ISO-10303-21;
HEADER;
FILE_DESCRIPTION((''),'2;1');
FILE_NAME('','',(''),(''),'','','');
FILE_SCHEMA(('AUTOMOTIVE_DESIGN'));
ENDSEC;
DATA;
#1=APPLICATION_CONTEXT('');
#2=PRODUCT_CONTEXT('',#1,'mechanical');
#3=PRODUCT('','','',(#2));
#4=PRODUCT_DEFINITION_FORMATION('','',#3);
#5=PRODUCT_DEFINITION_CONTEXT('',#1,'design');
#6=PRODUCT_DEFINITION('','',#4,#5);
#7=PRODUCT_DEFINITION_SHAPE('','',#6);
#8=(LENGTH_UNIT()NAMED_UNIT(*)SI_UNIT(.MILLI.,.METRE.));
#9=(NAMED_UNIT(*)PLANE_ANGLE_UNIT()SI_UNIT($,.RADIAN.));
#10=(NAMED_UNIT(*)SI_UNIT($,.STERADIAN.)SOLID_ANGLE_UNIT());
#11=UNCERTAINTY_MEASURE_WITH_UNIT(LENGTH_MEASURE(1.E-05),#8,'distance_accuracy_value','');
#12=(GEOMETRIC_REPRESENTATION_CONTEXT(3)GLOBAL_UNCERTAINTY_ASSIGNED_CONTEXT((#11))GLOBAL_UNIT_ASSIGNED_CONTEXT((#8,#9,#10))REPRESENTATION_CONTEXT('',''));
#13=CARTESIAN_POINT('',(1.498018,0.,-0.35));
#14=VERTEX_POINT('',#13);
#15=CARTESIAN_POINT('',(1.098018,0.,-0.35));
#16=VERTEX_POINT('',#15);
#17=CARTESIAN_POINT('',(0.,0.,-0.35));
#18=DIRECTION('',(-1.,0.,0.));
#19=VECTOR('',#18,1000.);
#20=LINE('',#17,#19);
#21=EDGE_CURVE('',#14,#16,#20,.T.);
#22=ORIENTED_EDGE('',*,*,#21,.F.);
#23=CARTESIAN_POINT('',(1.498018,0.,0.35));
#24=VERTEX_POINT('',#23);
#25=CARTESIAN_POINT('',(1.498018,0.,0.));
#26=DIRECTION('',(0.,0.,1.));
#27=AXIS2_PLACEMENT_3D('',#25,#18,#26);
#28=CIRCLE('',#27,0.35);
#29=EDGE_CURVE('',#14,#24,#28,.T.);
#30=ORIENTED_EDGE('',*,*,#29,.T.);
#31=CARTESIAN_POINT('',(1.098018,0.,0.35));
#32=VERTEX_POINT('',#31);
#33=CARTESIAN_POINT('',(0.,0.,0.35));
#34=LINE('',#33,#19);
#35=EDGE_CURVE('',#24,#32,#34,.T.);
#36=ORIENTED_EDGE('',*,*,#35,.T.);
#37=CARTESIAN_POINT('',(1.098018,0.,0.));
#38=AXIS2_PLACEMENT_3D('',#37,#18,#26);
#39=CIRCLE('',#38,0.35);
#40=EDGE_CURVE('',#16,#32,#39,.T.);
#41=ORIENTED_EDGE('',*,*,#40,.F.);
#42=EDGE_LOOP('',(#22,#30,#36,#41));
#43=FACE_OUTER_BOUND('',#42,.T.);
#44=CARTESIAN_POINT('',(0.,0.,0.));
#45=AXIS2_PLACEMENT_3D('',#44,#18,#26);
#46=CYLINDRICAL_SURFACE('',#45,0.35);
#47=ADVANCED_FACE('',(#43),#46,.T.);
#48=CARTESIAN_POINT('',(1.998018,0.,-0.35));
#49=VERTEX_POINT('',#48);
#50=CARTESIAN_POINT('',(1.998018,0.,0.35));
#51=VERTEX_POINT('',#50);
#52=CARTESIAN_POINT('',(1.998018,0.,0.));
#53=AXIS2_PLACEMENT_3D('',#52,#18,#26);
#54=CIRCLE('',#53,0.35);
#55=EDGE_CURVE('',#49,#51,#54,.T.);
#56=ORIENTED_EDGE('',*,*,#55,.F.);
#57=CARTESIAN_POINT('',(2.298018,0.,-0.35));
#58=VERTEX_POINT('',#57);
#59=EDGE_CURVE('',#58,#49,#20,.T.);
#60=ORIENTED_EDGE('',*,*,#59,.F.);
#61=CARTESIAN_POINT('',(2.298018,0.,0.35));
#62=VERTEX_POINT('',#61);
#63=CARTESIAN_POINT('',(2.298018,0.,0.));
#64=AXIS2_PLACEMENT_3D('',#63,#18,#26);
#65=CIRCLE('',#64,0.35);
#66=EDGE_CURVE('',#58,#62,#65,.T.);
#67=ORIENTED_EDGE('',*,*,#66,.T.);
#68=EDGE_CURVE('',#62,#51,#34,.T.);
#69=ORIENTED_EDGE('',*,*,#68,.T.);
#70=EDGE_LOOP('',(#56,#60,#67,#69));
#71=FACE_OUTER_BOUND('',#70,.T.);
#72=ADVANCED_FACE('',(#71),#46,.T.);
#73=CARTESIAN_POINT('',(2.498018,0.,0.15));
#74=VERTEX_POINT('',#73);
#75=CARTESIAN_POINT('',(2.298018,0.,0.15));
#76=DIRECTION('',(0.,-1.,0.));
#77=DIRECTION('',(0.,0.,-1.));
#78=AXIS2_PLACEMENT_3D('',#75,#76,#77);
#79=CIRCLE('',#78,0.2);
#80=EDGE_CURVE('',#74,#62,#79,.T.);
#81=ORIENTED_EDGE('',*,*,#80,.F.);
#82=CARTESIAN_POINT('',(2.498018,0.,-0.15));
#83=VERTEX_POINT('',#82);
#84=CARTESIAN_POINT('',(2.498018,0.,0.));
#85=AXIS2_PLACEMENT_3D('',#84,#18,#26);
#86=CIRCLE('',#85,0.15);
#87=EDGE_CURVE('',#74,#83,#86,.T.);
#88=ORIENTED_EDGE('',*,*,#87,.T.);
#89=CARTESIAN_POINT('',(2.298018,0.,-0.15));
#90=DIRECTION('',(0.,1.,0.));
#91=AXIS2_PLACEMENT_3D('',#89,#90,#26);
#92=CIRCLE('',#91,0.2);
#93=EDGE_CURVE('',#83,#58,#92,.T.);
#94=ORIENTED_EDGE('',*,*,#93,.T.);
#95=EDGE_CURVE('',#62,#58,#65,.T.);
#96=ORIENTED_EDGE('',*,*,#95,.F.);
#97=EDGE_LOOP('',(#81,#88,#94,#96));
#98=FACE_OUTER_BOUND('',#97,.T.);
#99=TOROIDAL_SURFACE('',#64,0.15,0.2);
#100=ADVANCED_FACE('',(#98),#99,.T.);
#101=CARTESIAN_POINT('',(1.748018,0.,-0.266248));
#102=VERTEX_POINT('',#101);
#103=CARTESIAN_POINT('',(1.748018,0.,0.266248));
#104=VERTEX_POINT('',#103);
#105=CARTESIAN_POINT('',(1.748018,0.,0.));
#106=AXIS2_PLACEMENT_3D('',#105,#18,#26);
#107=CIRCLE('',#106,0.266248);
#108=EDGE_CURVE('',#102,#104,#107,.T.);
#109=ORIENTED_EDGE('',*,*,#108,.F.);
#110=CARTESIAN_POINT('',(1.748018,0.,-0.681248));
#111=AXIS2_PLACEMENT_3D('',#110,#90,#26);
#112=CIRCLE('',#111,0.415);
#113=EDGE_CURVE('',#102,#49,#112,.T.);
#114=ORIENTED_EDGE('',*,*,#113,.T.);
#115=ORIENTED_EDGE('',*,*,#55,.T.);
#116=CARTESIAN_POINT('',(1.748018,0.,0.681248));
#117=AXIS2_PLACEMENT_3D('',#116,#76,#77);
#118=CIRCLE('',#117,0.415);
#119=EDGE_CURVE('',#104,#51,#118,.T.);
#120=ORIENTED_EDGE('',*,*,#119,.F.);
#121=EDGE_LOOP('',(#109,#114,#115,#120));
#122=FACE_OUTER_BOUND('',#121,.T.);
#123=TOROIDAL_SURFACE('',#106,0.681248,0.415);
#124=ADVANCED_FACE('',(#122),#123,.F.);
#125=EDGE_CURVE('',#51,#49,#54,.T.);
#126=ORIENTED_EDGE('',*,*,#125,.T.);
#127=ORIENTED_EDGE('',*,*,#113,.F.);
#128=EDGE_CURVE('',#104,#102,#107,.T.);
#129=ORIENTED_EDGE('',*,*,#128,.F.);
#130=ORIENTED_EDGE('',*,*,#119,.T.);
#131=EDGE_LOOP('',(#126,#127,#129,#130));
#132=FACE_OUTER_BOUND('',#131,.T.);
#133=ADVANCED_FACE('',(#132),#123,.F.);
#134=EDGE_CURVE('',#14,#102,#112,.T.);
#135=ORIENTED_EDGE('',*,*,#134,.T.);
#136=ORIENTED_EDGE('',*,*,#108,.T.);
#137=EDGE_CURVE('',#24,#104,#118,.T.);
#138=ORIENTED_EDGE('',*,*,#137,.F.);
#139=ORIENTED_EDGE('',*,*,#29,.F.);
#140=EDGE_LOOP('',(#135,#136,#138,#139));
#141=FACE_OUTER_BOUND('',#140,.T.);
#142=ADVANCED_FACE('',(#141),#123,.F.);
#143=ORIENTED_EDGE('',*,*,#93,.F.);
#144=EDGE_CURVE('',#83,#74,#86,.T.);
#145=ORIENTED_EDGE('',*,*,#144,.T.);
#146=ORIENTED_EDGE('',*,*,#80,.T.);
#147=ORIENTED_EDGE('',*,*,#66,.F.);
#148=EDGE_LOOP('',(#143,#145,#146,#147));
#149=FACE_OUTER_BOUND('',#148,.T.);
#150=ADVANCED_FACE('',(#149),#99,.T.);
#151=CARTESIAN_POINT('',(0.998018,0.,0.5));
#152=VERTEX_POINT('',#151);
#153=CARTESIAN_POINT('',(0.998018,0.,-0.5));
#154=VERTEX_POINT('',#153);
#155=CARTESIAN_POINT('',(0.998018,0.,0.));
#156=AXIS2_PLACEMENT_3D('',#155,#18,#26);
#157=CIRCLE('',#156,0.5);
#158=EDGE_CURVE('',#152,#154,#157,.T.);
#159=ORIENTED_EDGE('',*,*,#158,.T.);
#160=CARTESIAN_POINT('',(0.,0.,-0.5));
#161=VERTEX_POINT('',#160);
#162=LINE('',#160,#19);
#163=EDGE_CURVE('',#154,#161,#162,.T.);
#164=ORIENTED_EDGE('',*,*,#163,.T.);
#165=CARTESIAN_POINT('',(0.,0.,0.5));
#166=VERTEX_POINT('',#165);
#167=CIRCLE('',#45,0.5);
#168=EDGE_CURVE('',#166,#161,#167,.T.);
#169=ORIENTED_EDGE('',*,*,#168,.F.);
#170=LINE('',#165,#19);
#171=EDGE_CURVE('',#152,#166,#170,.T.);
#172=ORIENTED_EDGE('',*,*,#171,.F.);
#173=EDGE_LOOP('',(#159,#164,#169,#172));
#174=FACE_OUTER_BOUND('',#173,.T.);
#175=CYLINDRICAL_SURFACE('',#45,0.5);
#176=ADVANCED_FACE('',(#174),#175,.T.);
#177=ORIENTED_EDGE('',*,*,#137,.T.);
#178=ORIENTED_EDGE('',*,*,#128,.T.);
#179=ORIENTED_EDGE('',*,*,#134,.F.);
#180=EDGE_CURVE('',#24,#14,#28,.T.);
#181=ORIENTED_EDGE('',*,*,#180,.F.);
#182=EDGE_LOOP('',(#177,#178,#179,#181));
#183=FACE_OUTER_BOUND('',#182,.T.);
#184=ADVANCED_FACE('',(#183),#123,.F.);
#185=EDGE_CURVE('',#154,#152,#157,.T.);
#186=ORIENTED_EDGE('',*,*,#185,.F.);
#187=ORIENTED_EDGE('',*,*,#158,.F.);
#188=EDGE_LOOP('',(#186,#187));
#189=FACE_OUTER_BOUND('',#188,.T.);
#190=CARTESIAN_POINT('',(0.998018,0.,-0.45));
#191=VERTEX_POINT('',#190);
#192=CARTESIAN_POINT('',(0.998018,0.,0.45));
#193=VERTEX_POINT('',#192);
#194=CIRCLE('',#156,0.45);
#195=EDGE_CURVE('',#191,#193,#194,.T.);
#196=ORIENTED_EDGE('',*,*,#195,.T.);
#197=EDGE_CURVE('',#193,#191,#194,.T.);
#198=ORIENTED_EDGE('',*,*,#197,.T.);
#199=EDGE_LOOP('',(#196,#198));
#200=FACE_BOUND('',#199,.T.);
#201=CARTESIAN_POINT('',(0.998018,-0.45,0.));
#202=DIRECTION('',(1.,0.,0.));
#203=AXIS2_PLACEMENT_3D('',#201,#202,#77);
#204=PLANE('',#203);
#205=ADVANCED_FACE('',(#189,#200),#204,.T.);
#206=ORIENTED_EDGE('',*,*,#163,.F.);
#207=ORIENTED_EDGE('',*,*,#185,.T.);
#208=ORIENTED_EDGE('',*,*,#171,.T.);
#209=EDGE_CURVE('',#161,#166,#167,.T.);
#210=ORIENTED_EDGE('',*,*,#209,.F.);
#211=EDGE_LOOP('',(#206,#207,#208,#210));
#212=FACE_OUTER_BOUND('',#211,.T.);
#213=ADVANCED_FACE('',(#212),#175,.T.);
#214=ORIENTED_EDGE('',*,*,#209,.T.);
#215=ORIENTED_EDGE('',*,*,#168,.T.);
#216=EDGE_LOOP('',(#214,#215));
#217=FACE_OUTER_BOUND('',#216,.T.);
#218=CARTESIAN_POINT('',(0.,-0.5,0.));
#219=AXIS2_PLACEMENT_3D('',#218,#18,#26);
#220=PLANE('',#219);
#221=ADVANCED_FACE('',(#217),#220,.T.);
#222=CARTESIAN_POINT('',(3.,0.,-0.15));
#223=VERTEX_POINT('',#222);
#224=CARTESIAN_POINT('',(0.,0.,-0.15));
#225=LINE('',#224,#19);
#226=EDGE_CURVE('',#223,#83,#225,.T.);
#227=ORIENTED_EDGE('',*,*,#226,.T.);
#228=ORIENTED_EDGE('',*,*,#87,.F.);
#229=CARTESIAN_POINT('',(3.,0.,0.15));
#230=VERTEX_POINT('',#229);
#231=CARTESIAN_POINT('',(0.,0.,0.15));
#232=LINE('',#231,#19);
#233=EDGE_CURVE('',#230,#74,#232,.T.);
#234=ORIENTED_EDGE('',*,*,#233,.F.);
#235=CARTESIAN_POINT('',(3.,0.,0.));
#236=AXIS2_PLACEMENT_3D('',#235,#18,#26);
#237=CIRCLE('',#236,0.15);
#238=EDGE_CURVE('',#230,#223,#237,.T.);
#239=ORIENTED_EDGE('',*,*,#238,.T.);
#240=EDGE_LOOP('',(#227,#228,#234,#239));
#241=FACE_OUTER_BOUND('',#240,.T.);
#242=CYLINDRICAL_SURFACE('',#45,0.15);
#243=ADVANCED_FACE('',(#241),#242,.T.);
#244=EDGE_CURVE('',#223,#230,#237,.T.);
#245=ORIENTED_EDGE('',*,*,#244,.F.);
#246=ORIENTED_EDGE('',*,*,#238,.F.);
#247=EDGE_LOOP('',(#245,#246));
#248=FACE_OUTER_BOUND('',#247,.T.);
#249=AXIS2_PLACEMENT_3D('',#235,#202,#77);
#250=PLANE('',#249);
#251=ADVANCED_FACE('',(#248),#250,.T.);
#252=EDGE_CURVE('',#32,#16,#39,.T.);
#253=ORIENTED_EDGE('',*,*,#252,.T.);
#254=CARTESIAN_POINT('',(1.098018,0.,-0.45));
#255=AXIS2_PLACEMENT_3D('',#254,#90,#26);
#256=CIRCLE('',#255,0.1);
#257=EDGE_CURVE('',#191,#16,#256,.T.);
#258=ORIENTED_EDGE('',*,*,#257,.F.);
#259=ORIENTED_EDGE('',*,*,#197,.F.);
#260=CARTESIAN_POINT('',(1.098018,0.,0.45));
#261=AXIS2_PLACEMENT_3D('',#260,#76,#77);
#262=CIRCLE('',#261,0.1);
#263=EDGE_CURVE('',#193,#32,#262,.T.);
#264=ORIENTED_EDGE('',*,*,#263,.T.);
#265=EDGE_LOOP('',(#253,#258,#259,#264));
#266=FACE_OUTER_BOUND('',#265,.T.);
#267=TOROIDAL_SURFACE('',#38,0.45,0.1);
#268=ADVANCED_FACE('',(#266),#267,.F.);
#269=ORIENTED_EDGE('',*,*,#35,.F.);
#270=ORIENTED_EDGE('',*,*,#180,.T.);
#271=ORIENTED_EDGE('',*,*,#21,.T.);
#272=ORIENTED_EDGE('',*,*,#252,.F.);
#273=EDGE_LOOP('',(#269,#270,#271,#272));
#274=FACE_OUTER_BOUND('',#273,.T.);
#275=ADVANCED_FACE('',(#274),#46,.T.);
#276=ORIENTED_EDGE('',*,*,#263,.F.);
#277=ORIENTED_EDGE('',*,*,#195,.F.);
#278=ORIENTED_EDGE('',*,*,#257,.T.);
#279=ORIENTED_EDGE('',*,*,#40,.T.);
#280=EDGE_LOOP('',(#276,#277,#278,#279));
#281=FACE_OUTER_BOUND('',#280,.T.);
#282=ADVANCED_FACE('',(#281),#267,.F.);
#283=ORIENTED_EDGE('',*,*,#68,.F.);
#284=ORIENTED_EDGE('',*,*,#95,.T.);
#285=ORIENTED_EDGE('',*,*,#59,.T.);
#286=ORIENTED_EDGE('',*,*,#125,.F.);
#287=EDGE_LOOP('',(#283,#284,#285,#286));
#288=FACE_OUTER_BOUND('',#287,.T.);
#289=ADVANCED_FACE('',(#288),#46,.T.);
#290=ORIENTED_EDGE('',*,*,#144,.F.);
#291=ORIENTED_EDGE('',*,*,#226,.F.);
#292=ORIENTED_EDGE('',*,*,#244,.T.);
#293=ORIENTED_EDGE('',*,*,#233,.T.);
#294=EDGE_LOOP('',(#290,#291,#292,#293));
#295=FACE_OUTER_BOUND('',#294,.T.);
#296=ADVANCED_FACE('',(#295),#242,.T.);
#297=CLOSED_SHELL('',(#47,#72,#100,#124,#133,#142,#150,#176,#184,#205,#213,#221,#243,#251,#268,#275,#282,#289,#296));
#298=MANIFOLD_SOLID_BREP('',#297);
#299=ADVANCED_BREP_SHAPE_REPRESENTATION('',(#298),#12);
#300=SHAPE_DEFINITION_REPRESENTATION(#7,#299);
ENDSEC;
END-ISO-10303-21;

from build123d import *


with BuildPart() as part:
    # Pin Profile Sketch → Stepped Pin Revolve (revolve)
    with BuildSketch(Plane.XY, mode=Mode.PRIVATE) as stepped_pin_revolve_sk:
        with BuildLine():
            Line((3, 0), (3, -0.15))
            Line((3, -0.15), (2.498017858, -0.15))
            ThreePointArc((2.498017858, -0.15), (2.439439214, -0.291421356), (2.298017858, -0.35))
            Line((2.298017858, -0.35), (1.998017858, -0.35))
            ThreePointArc((1.998017858, -0.35), (1.748017858, -0.266247642), (1.498017858, -0.35))
            Line((1.498017858, -0.35), (1.098017858, -0.35))
            ThreePointArc((1.098017858, -0.35), (1.02730718, -0.379289322), (0.998017858, -0.45))
            Line((0.998017858, -0.45), (0.998017858, -0.5))
            Line((0.998017858, -0.5), (0, -0.5))
            Line((0, -0.5), (0, 0))
            Line((0, 0), (3, 0))
        make_face()
    revolve(stepped_pin_revolve_sk.sketch.rotate(Axis((0, 0, 0), (1, 0, 0)), 270), axis=Axis((0, 0, 0), (1, 0, 0)))


solid = part.part
